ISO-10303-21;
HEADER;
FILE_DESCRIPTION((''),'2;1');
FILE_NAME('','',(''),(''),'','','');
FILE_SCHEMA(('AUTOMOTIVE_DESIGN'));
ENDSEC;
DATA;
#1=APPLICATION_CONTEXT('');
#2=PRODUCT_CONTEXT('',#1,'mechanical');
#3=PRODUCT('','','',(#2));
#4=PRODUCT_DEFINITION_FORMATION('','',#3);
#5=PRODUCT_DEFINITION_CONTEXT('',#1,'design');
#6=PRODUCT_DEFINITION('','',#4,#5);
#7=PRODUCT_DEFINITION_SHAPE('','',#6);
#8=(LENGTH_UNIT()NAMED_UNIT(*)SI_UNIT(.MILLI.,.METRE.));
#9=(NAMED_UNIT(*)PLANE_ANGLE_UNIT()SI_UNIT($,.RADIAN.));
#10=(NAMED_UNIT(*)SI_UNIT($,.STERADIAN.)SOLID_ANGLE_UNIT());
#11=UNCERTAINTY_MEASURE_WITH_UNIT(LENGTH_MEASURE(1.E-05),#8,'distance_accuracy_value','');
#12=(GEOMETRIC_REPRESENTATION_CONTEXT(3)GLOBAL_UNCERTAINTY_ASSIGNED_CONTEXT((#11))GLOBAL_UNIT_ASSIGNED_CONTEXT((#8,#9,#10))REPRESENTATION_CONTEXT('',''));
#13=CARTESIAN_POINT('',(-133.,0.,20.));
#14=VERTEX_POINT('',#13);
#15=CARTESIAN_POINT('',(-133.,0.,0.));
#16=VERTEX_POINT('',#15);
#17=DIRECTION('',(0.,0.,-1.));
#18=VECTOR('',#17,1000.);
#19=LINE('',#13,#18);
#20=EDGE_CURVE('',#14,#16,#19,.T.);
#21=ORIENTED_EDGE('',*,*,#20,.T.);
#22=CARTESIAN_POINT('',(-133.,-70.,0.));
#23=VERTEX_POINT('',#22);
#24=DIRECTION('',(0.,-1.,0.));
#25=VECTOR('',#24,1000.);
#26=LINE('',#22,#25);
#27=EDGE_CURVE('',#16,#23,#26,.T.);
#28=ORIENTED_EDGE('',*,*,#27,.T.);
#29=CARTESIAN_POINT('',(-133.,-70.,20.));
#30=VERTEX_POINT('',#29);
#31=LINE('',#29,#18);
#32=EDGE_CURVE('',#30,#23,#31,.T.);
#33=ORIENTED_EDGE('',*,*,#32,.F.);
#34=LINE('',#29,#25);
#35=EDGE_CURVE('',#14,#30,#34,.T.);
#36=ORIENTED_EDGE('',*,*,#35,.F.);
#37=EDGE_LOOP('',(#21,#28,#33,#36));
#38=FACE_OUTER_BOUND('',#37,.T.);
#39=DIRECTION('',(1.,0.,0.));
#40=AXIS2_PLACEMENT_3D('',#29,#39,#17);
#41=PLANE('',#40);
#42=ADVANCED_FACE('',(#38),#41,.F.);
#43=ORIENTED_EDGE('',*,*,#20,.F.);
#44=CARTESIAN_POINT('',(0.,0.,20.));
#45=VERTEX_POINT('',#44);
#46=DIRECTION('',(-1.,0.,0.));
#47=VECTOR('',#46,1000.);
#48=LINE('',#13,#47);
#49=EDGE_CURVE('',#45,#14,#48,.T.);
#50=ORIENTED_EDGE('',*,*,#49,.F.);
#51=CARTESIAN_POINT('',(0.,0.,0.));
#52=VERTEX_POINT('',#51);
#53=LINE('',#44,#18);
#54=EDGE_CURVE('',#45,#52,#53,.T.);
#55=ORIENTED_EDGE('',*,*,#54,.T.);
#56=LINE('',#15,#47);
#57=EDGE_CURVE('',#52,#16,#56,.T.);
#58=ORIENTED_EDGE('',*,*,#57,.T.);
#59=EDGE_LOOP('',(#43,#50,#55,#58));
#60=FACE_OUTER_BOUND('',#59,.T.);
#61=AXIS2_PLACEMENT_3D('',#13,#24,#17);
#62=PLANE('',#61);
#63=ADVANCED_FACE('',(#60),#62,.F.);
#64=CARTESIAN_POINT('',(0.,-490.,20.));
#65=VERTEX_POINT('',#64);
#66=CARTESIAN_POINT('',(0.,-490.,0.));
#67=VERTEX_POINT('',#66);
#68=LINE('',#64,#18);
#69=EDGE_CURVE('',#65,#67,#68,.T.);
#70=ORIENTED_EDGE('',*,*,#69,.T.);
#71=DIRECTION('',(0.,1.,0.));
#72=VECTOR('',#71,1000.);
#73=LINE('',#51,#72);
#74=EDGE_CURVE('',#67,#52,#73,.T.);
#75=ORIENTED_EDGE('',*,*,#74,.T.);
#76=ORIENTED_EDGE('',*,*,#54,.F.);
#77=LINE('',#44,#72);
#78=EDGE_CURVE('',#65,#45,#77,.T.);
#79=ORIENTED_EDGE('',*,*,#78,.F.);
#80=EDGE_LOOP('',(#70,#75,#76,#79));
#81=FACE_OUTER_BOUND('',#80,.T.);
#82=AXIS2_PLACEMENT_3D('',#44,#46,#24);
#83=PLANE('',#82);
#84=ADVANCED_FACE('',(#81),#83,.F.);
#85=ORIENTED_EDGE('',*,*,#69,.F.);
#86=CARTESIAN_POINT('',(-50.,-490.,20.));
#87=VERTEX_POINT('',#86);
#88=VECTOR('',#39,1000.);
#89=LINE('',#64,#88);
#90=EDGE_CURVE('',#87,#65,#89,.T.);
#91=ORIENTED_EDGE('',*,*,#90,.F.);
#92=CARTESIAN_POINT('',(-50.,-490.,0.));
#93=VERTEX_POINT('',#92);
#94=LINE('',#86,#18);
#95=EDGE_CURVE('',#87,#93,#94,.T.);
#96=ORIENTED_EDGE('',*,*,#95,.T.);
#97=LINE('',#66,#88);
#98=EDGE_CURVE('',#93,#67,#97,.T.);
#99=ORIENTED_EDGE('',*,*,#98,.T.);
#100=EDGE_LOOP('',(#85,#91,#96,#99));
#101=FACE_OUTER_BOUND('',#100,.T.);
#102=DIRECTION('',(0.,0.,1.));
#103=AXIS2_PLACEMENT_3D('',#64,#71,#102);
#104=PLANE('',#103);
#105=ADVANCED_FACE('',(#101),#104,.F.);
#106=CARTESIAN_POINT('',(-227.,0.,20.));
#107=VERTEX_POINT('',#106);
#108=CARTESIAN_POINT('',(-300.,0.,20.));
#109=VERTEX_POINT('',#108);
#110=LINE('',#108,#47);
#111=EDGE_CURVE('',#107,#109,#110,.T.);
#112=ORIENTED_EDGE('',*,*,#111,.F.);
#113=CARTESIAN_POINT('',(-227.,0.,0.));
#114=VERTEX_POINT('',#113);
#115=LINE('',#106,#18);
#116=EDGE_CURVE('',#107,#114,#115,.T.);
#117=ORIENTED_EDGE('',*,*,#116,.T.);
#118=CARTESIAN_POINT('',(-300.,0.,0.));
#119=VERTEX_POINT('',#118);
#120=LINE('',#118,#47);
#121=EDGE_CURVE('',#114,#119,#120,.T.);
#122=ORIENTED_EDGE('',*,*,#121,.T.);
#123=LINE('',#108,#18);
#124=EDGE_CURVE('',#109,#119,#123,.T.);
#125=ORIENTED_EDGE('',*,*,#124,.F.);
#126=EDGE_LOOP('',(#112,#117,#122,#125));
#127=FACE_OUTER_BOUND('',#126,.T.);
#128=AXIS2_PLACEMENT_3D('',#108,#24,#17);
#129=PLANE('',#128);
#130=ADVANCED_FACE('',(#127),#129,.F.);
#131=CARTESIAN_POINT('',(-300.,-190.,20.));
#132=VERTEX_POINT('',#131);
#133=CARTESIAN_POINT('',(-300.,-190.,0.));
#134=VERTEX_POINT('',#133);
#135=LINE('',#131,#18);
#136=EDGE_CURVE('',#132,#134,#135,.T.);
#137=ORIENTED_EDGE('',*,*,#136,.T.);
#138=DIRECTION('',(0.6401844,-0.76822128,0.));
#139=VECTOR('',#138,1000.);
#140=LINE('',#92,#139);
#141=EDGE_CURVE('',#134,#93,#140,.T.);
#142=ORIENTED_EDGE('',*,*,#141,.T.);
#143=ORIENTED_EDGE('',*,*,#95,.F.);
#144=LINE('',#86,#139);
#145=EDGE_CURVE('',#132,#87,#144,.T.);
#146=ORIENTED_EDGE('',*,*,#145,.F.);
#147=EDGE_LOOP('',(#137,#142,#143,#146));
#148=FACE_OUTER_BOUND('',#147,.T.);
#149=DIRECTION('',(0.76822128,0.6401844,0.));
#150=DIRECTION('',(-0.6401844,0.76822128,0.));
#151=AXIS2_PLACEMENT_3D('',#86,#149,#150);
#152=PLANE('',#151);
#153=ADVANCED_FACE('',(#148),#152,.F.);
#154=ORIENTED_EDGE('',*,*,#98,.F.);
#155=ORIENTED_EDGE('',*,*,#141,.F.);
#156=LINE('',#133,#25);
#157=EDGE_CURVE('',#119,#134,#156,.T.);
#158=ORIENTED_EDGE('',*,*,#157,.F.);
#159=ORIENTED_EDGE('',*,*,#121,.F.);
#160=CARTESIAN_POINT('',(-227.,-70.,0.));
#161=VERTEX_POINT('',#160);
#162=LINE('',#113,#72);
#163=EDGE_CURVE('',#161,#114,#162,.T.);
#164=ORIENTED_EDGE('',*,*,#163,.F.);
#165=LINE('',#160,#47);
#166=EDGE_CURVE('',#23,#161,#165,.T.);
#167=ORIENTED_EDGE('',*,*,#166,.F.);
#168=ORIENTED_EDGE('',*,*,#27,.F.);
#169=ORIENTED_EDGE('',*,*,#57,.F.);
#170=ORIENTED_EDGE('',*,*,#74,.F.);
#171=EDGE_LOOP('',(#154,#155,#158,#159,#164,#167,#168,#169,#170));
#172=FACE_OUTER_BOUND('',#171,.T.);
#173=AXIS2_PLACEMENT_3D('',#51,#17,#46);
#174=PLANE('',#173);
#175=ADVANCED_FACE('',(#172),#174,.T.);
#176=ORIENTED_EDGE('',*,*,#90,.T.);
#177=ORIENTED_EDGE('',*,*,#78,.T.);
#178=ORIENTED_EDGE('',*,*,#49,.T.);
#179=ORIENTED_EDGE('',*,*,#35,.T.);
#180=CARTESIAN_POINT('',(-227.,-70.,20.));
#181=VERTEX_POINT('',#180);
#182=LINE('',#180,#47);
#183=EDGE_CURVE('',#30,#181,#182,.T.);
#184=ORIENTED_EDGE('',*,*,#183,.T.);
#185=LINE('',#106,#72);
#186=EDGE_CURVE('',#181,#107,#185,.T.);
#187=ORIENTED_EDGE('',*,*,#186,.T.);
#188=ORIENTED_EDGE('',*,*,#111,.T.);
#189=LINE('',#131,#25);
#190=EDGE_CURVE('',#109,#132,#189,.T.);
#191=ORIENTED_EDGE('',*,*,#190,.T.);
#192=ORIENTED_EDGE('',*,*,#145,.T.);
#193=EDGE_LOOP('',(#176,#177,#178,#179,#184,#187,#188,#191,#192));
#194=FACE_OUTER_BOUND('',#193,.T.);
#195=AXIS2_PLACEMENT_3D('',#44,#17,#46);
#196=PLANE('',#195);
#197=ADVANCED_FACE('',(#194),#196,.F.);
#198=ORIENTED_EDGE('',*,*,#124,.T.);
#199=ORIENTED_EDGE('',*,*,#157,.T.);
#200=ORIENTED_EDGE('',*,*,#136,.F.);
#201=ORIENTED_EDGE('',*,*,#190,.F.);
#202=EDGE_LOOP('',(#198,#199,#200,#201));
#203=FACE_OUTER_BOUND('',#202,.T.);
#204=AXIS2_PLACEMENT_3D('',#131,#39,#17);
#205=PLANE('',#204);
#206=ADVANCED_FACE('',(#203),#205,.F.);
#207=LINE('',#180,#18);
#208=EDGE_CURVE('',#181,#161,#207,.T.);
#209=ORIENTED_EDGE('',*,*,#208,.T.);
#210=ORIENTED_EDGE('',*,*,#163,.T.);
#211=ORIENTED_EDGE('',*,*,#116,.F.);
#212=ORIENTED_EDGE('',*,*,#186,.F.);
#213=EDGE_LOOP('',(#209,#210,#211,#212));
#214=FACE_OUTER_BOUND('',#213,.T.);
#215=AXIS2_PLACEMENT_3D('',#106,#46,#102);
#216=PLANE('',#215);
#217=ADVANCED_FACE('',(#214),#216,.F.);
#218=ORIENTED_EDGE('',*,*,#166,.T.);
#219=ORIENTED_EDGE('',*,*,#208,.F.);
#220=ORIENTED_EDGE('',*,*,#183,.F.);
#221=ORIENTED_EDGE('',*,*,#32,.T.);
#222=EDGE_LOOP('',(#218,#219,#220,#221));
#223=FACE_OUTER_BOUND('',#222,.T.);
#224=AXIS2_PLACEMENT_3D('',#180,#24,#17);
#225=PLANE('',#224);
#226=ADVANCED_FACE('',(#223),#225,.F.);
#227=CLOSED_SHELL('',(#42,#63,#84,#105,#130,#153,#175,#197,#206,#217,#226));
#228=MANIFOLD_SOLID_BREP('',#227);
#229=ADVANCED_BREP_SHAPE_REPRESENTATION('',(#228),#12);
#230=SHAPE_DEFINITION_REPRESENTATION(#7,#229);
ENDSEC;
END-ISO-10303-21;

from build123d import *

# Parameters (mm, degrees)
BOSS_EXTRUDE1_DEPTH = 20


with BuildPart() as part:
    # Sketch1 → Boss-Extrude1 (new body)
    with BuildSketch(Plane.XY):
        Polygon((0, 0), (0, -490), (-50, -490), (-300, -190), (-300, 0), (-227, 0), (-227, -70), (-133, -70), (-133, 0), align=None)
    extrude(amount=BOSS_EXTRUDE1_DEPTH)


solid = part.part
